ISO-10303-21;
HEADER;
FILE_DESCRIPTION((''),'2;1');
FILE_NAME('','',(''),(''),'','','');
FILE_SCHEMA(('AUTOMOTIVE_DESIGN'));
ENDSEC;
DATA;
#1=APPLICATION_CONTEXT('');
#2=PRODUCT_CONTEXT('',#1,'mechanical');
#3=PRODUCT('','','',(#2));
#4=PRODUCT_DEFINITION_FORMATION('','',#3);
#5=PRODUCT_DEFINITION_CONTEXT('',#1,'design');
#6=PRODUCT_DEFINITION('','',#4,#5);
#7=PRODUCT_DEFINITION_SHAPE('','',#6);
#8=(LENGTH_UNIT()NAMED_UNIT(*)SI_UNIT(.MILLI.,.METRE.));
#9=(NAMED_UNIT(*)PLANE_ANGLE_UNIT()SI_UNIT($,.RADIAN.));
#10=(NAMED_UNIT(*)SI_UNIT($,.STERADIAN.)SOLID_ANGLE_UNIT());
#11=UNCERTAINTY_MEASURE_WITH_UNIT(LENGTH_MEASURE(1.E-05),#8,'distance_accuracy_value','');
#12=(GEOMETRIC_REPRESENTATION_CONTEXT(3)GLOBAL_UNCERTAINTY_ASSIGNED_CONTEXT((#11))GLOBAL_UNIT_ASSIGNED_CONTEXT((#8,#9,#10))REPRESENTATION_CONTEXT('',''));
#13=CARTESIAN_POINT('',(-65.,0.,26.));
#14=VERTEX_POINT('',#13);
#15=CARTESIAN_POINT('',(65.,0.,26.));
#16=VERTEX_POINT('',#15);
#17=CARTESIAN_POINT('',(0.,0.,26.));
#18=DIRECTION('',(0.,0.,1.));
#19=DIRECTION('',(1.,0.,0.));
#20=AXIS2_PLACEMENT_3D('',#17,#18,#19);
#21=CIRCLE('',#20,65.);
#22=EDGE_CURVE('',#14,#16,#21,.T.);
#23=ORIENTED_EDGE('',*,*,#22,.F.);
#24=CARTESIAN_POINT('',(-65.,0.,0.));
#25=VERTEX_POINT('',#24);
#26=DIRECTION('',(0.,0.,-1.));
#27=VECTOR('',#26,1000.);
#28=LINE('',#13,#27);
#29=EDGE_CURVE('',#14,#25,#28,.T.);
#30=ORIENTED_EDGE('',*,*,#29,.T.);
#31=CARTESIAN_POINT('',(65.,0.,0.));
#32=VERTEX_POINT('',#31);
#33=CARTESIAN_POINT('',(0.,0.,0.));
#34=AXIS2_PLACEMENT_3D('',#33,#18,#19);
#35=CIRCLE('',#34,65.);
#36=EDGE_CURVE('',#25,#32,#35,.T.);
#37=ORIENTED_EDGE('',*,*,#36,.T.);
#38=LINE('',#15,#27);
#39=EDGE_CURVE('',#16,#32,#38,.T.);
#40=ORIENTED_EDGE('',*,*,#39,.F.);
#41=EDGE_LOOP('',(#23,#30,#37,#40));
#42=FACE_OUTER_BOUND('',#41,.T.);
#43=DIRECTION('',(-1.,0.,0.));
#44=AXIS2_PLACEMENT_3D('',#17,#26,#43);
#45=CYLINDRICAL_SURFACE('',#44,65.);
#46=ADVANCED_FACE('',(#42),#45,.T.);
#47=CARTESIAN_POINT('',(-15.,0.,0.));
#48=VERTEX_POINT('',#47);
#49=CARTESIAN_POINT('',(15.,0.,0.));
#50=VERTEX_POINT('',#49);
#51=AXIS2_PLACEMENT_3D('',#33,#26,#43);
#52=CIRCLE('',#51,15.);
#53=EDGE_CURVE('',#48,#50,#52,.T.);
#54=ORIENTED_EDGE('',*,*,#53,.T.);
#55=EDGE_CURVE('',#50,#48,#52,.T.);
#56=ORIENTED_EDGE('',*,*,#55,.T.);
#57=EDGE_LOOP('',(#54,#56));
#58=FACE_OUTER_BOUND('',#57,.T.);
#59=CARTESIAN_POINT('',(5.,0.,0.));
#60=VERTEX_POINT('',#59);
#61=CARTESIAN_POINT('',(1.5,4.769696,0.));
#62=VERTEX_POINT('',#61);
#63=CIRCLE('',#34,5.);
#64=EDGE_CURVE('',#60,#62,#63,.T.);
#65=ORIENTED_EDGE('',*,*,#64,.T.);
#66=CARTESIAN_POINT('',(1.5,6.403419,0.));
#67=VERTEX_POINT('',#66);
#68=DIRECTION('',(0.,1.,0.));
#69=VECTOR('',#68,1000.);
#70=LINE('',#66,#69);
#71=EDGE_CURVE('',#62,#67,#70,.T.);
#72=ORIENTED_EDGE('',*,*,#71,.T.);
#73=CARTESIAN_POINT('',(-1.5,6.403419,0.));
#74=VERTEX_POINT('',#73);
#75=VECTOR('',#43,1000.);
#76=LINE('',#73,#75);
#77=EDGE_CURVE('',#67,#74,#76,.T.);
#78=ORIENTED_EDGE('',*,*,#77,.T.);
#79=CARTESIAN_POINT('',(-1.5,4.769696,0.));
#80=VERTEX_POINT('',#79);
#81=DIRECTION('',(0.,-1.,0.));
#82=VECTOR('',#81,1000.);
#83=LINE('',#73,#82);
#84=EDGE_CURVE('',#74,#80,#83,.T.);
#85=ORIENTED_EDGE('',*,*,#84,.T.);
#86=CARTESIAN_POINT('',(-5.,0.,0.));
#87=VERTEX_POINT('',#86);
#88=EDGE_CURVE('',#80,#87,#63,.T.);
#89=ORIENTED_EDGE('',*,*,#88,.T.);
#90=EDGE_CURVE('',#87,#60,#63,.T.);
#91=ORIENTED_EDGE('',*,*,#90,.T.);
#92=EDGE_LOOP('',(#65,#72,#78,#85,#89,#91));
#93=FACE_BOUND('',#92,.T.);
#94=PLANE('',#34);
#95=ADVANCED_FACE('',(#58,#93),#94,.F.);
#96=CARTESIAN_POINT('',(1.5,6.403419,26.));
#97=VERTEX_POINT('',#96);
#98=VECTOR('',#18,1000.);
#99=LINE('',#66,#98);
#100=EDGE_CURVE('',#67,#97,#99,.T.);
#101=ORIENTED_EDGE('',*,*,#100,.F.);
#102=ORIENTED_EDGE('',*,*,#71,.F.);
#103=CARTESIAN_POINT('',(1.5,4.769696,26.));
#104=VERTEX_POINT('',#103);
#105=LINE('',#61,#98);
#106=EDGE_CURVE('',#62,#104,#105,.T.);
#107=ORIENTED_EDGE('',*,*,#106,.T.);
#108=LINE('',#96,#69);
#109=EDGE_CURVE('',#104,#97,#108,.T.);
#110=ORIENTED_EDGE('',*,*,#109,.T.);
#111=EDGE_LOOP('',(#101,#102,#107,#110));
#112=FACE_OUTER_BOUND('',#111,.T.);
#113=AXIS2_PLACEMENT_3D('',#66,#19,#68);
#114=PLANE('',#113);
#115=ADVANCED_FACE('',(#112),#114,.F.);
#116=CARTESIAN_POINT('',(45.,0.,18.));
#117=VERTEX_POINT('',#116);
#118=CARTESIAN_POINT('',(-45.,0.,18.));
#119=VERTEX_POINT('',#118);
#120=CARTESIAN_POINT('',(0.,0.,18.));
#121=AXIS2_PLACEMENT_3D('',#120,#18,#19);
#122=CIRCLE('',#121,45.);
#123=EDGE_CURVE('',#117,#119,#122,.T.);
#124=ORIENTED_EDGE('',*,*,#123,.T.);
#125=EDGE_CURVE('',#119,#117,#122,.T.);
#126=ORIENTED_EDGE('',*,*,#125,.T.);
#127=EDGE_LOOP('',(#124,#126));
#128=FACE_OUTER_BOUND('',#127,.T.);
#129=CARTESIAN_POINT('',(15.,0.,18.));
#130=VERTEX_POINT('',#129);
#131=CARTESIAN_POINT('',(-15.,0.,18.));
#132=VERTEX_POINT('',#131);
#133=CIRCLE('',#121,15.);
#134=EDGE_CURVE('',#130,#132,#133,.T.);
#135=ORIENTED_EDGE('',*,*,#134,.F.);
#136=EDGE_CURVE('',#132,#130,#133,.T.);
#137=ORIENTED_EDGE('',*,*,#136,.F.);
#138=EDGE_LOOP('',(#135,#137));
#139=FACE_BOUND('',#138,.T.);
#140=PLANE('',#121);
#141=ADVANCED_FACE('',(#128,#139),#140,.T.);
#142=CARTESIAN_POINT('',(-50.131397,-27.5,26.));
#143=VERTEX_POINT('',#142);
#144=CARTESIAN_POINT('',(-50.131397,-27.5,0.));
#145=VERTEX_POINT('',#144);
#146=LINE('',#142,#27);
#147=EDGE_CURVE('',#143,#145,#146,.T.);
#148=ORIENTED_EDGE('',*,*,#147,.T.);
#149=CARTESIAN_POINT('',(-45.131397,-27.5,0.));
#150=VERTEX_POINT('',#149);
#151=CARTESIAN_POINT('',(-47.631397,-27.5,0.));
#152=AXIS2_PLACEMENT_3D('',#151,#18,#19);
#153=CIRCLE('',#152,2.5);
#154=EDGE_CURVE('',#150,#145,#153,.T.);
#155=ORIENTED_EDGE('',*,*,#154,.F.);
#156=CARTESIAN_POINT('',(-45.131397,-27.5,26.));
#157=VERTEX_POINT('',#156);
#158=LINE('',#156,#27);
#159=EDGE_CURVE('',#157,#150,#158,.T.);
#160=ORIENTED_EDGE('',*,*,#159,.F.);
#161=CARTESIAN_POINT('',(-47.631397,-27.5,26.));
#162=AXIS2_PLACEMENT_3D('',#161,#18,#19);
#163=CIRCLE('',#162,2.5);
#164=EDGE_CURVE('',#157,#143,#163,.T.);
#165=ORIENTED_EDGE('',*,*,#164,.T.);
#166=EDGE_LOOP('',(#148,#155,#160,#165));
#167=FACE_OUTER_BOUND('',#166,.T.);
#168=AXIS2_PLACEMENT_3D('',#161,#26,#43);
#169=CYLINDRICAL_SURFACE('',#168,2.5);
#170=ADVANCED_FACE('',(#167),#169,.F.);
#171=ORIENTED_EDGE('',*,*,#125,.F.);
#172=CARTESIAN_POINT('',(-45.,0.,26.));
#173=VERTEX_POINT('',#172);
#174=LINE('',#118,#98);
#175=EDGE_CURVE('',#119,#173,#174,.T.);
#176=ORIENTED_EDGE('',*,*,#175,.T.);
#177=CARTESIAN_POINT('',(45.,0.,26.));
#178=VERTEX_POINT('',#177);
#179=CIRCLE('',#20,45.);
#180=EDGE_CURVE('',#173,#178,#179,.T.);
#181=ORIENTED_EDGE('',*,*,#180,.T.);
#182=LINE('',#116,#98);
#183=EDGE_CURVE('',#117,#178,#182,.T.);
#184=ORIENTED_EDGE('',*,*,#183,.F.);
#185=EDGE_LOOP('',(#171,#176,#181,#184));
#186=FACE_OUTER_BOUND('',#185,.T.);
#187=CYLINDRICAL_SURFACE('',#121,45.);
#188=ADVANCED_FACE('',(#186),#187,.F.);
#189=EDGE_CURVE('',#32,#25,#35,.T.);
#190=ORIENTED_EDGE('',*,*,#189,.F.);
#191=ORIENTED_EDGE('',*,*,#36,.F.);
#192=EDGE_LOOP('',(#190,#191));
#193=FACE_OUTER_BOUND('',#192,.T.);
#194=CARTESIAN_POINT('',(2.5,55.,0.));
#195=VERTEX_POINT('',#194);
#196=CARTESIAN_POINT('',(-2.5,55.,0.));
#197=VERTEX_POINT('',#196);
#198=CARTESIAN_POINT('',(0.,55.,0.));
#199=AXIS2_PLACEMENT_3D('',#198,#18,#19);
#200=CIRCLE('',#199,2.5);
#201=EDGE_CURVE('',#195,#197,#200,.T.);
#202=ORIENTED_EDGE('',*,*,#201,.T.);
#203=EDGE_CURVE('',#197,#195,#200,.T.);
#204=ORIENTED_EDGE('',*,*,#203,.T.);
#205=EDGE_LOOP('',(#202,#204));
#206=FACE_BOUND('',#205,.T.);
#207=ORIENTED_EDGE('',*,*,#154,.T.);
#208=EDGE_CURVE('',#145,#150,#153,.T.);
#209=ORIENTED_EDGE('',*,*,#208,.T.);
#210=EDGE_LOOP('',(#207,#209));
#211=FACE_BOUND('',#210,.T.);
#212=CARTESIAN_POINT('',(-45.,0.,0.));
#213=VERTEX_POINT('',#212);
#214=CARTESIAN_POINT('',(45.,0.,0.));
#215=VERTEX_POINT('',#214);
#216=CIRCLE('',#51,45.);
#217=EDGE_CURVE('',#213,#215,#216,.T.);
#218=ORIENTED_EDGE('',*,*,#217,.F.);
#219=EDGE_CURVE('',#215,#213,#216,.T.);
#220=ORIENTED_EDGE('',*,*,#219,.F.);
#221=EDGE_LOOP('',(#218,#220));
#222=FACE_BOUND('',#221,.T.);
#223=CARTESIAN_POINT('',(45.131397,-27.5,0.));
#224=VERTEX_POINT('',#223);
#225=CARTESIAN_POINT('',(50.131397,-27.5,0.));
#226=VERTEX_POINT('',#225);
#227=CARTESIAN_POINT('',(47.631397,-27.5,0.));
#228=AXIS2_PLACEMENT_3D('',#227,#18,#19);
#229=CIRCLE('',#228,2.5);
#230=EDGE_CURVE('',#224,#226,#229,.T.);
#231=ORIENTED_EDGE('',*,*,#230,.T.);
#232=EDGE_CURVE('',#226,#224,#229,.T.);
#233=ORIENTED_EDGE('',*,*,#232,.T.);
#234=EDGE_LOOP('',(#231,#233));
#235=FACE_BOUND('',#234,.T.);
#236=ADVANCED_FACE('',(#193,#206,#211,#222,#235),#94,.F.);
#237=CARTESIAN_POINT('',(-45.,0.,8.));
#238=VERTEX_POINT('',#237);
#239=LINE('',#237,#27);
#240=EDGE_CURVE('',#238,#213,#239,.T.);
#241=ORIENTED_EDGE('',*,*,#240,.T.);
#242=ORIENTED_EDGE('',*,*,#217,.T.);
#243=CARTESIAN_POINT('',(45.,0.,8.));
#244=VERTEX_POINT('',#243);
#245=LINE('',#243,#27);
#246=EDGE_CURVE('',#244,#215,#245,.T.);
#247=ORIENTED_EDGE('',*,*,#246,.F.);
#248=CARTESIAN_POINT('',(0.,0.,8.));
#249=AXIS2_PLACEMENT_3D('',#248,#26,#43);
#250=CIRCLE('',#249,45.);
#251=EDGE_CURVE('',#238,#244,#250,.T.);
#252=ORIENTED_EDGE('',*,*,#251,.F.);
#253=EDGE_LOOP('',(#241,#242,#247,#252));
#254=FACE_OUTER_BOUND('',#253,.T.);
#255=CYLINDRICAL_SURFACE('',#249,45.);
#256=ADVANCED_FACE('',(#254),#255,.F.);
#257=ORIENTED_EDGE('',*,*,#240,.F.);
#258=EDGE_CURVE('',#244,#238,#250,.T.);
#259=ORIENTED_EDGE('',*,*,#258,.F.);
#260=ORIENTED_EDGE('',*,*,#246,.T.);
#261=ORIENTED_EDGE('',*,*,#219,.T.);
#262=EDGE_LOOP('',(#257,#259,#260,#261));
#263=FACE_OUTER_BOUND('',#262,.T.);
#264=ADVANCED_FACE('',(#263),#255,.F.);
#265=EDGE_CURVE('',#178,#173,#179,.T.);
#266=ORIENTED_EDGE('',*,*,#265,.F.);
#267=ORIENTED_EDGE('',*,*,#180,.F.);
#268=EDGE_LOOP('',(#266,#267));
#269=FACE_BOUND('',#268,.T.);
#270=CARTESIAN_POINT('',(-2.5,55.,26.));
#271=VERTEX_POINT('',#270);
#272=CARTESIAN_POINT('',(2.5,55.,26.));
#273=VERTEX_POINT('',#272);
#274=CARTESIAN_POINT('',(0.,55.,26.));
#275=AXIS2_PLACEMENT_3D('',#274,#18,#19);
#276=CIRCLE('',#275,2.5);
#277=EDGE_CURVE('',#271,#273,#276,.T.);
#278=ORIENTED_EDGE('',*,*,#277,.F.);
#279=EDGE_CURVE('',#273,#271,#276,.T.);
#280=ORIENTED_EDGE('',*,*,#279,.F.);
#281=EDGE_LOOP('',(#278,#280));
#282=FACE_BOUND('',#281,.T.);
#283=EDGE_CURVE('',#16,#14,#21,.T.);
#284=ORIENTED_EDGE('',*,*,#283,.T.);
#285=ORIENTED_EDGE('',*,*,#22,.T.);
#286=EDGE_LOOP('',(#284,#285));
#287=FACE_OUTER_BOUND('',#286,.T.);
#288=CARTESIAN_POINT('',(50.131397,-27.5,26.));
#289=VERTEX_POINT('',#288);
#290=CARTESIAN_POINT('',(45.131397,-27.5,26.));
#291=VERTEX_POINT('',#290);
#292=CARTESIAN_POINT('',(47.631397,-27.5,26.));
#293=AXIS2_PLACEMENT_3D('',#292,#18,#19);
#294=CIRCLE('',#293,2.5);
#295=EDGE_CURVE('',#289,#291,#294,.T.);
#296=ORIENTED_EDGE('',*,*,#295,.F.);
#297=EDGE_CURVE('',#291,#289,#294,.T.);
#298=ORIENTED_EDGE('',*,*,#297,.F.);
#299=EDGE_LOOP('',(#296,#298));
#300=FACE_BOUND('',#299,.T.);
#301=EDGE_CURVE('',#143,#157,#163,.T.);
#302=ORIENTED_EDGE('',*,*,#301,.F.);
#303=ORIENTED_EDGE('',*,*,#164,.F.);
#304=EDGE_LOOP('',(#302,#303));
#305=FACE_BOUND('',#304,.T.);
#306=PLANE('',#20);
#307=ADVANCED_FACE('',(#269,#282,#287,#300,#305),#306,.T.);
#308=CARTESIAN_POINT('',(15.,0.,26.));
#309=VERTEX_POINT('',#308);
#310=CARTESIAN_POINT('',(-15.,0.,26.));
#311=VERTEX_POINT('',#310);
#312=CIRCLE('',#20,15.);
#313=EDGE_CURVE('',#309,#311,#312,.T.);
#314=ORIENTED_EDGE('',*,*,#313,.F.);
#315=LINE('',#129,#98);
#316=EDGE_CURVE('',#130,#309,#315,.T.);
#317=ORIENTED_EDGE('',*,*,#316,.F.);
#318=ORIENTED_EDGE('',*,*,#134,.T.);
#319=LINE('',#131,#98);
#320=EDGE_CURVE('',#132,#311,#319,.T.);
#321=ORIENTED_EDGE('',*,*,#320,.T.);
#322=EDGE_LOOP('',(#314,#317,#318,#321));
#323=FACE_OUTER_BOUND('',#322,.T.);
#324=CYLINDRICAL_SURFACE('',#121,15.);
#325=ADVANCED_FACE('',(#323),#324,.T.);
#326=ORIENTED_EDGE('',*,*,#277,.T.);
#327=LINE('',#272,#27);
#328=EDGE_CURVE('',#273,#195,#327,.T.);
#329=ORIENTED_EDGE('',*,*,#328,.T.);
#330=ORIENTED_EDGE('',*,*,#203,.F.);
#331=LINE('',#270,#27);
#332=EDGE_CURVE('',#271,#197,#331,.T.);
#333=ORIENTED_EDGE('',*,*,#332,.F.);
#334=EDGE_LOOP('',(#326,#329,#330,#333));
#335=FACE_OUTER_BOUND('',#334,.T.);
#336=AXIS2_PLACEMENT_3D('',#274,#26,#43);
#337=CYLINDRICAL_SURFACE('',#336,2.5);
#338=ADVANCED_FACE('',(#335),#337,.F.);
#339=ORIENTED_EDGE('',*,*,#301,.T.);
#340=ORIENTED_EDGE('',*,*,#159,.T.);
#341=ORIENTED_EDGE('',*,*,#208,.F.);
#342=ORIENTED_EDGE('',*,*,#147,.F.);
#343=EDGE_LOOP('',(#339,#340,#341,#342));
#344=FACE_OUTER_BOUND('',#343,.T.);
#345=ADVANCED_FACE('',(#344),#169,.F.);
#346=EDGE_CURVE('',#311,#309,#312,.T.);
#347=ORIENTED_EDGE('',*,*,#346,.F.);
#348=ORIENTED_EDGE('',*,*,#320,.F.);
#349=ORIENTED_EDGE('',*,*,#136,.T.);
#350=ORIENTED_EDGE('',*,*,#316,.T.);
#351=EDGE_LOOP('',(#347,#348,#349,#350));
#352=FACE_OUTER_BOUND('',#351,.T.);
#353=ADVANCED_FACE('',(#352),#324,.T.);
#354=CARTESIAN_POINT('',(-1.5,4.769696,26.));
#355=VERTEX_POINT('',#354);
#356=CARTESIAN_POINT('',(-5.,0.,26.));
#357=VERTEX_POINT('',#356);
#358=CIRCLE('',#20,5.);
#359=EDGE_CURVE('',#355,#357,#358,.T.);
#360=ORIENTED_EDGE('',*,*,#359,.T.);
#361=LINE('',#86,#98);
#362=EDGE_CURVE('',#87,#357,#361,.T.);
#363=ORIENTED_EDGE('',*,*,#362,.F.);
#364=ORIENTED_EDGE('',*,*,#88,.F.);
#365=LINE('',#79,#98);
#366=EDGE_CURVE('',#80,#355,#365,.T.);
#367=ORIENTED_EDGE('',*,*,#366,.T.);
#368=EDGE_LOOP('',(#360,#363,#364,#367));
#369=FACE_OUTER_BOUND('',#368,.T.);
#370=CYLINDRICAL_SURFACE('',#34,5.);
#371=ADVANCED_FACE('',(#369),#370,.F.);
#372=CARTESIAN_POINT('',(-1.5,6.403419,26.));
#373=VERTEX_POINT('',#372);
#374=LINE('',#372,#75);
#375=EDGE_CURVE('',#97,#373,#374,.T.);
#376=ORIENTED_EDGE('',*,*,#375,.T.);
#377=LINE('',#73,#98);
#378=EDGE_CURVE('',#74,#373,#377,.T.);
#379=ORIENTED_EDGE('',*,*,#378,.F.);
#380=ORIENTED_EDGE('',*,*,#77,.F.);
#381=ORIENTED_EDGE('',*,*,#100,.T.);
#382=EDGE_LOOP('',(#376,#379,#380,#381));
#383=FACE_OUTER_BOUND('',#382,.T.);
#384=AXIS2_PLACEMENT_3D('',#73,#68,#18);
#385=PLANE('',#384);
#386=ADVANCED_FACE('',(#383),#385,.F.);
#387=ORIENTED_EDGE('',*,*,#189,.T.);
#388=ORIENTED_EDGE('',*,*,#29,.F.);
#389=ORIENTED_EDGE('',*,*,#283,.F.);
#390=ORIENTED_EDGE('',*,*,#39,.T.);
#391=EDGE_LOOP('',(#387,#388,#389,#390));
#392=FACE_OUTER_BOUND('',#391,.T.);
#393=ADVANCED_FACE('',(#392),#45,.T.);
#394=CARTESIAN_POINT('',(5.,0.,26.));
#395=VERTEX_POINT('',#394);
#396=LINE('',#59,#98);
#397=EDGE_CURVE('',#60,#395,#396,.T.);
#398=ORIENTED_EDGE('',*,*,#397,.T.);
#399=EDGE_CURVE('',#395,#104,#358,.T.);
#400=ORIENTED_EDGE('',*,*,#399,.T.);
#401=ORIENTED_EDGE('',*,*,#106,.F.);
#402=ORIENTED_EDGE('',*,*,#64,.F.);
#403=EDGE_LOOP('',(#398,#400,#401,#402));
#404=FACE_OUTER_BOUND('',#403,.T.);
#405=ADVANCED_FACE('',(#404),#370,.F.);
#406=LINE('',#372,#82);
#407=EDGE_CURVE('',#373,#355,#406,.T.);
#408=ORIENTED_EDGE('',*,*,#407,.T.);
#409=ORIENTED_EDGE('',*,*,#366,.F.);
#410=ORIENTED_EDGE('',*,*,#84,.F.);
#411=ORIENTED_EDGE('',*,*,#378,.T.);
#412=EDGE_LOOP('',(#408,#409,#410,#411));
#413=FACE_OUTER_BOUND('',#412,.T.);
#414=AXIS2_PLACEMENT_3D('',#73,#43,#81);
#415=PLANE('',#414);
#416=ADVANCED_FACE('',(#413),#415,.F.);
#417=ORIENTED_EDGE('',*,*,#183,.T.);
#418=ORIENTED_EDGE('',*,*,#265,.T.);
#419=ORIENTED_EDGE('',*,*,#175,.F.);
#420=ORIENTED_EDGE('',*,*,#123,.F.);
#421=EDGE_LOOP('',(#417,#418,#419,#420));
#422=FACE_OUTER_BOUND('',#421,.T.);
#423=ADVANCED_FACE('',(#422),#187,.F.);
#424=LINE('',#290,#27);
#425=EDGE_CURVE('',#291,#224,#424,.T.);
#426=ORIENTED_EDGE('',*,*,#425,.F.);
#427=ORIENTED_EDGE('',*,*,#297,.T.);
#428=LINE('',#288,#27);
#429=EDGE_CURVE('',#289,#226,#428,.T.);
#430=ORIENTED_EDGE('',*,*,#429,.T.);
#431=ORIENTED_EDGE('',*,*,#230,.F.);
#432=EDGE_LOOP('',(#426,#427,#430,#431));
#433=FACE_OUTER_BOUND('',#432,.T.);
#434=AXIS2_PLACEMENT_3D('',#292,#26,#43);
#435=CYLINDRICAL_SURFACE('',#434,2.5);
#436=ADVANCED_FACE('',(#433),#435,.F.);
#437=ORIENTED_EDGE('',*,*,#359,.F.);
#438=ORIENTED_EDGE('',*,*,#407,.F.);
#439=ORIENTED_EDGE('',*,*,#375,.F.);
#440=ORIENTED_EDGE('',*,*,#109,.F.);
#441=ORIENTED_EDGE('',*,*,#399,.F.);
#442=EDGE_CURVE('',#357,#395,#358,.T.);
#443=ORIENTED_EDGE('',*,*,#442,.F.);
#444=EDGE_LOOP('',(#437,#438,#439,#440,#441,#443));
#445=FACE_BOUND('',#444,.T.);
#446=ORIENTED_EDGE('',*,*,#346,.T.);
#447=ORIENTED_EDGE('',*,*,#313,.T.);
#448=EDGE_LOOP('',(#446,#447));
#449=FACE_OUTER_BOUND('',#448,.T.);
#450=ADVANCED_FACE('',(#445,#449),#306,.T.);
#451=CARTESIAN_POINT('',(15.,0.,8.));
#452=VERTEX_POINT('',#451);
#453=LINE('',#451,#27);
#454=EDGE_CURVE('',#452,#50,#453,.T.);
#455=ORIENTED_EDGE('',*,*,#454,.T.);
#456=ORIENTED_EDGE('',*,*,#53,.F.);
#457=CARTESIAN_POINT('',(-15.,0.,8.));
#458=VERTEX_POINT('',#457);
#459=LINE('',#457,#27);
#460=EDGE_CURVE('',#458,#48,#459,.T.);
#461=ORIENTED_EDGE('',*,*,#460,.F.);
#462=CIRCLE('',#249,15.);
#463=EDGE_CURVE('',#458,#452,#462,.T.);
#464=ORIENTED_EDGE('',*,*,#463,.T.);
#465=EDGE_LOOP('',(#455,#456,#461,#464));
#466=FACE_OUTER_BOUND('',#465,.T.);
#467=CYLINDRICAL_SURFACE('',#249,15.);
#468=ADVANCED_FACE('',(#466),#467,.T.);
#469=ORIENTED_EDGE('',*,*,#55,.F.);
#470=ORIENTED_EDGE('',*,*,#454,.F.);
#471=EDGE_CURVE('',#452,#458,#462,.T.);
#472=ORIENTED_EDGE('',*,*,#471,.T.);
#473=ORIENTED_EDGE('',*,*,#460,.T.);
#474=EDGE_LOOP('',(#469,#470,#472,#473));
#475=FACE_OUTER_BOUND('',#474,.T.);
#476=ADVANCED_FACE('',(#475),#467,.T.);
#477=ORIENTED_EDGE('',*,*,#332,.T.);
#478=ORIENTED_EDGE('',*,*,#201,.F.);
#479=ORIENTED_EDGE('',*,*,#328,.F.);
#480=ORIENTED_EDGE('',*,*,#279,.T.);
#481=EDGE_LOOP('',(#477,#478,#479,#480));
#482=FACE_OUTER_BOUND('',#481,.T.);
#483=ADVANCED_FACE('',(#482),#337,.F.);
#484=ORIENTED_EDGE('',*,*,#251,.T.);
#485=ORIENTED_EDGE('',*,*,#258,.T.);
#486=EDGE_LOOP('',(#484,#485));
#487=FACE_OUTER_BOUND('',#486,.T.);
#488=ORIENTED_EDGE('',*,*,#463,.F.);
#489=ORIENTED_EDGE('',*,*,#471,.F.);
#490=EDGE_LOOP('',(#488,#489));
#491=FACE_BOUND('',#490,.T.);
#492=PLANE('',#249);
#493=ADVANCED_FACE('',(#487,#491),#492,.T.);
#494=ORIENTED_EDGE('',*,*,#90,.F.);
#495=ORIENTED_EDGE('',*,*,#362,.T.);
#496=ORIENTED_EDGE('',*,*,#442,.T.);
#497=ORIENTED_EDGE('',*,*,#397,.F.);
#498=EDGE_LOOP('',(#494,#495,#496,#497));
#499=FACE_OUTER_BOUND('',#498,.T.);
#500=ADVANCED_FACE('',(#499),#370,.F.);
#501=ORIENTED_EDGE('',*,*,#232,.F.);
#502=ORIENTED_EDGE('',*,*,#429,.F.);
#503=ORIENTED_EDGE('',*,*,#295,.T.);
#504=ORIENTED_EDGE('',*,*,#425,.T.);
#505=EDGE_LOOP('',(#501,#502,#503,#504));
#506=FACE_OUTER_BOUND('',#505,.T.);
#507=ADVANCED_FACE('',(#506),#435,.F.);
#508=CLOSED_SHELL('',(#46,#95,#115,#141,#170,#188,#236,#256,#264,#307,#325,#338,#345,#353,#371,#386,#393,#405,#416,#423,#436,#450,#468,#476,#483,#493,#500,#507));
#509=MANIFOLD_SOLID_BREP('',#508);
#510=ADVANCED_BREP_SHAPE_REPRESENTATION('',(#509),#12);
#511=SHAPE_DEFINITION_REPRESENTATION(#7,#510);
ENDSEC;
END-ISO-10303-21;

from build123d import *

# Parameters (mm, degrees)
SKETCH1_R           = 65
SKETCH1_R_2         = 2.5
BOSS_EXTRUDE1_DEPTH = 26
CUT_EXTRUDE1_DEPTH  = 96.530099969
SKETCH3_R           = 45
SKETCH3_R_2         = 15
CUT_EXTRUDE2_DEPTH  = 8
CUT_EXTRUDE3_START  = -8
SKETCH4_R           = 45
SKETCH4_R_2         = 15
CUT_EXTRUDE3_DEPTH  = 8


with BuildPart() as part:
    # Sketch1 → Boss-Extrude1 (new body)
    with BuildSketch(Plane.XY):
        with Locations(Location((0, 0, 0), (0, 0, 180))):
            Circle(SKETCH1_R)
        with Locations(Location((0, 55, 0), (0, 0, 180))):
            Circle(SKETCH1_R_2, mode=Mode.SUBTRACT)
        with Locations(Location((47.631397208, -27.5, 0), (0, 0, 180))):
            Circle(SKETCH1_R_2, mode=Mode.SUBTRACT)
        with Locations(Location((-47.631397208, -27.5, 0), (0, 0, 180))):
            Circle(SKETCH1_R_2, mode=Mode.SUBTRACT)
    extrude(amount=BOSS_EXTRUDE1_DEPTH)

    # Sketch2 → Cut-Extrude1 (cut, through all)
    with BuildSketch(Plane.XY.offset(26)):
        with BuildLine():
            Line((-1.5, 6.403418514), (1.5, 6.403418514))
            Line((1.5, 6.403418514), (1.5, 4.769696007))
            ThreePointArc((1.5, 4.769696007), (0, -5), (-1.5, 4.769696007))
            Line((-1.5, 4.769696007), (-1.5, 6.403418514))
        make_face()
    extrude(amount=-CUT_EXTRUDE1_DEPTH, mode=Mode.SUBTRACT)

    # Sketch3 → Cut-Extrude2 (cut)
    with BuildSketch(Plane.XY.offset(26)):
        Circle(SKETCH3_R)
        Circle(SKETCH3_R_2, mode=Mode.SUBTRACT)
    extrude(amount=-CUT_EXTRUDE2_DEPTH, mode=Mode.SUBTRACT)

    # Sketch4 → Cut-Extrude3 (cut)
    with BuildSketch(Plane(origin=(0, 0, 0), x_dir=(-1, 0, 0), z_dir=(0, 0, -1)).offset(CUT_EXTRUDE3_START)):
        with Locations(Location((0, 0, 0), (0, 0, 180))):
            Circle(SKETCH4_R)
        with Locations(Location((0, 0, 0), (0, 0, 180))):
            Circle(SKETCH4_R_2, mode=Mode.SUBTRACT)
    extrude(amount=CUT_EXTRUDE3_DEPTH, mode=Mode.SUBTRACT)


solid = part.part
